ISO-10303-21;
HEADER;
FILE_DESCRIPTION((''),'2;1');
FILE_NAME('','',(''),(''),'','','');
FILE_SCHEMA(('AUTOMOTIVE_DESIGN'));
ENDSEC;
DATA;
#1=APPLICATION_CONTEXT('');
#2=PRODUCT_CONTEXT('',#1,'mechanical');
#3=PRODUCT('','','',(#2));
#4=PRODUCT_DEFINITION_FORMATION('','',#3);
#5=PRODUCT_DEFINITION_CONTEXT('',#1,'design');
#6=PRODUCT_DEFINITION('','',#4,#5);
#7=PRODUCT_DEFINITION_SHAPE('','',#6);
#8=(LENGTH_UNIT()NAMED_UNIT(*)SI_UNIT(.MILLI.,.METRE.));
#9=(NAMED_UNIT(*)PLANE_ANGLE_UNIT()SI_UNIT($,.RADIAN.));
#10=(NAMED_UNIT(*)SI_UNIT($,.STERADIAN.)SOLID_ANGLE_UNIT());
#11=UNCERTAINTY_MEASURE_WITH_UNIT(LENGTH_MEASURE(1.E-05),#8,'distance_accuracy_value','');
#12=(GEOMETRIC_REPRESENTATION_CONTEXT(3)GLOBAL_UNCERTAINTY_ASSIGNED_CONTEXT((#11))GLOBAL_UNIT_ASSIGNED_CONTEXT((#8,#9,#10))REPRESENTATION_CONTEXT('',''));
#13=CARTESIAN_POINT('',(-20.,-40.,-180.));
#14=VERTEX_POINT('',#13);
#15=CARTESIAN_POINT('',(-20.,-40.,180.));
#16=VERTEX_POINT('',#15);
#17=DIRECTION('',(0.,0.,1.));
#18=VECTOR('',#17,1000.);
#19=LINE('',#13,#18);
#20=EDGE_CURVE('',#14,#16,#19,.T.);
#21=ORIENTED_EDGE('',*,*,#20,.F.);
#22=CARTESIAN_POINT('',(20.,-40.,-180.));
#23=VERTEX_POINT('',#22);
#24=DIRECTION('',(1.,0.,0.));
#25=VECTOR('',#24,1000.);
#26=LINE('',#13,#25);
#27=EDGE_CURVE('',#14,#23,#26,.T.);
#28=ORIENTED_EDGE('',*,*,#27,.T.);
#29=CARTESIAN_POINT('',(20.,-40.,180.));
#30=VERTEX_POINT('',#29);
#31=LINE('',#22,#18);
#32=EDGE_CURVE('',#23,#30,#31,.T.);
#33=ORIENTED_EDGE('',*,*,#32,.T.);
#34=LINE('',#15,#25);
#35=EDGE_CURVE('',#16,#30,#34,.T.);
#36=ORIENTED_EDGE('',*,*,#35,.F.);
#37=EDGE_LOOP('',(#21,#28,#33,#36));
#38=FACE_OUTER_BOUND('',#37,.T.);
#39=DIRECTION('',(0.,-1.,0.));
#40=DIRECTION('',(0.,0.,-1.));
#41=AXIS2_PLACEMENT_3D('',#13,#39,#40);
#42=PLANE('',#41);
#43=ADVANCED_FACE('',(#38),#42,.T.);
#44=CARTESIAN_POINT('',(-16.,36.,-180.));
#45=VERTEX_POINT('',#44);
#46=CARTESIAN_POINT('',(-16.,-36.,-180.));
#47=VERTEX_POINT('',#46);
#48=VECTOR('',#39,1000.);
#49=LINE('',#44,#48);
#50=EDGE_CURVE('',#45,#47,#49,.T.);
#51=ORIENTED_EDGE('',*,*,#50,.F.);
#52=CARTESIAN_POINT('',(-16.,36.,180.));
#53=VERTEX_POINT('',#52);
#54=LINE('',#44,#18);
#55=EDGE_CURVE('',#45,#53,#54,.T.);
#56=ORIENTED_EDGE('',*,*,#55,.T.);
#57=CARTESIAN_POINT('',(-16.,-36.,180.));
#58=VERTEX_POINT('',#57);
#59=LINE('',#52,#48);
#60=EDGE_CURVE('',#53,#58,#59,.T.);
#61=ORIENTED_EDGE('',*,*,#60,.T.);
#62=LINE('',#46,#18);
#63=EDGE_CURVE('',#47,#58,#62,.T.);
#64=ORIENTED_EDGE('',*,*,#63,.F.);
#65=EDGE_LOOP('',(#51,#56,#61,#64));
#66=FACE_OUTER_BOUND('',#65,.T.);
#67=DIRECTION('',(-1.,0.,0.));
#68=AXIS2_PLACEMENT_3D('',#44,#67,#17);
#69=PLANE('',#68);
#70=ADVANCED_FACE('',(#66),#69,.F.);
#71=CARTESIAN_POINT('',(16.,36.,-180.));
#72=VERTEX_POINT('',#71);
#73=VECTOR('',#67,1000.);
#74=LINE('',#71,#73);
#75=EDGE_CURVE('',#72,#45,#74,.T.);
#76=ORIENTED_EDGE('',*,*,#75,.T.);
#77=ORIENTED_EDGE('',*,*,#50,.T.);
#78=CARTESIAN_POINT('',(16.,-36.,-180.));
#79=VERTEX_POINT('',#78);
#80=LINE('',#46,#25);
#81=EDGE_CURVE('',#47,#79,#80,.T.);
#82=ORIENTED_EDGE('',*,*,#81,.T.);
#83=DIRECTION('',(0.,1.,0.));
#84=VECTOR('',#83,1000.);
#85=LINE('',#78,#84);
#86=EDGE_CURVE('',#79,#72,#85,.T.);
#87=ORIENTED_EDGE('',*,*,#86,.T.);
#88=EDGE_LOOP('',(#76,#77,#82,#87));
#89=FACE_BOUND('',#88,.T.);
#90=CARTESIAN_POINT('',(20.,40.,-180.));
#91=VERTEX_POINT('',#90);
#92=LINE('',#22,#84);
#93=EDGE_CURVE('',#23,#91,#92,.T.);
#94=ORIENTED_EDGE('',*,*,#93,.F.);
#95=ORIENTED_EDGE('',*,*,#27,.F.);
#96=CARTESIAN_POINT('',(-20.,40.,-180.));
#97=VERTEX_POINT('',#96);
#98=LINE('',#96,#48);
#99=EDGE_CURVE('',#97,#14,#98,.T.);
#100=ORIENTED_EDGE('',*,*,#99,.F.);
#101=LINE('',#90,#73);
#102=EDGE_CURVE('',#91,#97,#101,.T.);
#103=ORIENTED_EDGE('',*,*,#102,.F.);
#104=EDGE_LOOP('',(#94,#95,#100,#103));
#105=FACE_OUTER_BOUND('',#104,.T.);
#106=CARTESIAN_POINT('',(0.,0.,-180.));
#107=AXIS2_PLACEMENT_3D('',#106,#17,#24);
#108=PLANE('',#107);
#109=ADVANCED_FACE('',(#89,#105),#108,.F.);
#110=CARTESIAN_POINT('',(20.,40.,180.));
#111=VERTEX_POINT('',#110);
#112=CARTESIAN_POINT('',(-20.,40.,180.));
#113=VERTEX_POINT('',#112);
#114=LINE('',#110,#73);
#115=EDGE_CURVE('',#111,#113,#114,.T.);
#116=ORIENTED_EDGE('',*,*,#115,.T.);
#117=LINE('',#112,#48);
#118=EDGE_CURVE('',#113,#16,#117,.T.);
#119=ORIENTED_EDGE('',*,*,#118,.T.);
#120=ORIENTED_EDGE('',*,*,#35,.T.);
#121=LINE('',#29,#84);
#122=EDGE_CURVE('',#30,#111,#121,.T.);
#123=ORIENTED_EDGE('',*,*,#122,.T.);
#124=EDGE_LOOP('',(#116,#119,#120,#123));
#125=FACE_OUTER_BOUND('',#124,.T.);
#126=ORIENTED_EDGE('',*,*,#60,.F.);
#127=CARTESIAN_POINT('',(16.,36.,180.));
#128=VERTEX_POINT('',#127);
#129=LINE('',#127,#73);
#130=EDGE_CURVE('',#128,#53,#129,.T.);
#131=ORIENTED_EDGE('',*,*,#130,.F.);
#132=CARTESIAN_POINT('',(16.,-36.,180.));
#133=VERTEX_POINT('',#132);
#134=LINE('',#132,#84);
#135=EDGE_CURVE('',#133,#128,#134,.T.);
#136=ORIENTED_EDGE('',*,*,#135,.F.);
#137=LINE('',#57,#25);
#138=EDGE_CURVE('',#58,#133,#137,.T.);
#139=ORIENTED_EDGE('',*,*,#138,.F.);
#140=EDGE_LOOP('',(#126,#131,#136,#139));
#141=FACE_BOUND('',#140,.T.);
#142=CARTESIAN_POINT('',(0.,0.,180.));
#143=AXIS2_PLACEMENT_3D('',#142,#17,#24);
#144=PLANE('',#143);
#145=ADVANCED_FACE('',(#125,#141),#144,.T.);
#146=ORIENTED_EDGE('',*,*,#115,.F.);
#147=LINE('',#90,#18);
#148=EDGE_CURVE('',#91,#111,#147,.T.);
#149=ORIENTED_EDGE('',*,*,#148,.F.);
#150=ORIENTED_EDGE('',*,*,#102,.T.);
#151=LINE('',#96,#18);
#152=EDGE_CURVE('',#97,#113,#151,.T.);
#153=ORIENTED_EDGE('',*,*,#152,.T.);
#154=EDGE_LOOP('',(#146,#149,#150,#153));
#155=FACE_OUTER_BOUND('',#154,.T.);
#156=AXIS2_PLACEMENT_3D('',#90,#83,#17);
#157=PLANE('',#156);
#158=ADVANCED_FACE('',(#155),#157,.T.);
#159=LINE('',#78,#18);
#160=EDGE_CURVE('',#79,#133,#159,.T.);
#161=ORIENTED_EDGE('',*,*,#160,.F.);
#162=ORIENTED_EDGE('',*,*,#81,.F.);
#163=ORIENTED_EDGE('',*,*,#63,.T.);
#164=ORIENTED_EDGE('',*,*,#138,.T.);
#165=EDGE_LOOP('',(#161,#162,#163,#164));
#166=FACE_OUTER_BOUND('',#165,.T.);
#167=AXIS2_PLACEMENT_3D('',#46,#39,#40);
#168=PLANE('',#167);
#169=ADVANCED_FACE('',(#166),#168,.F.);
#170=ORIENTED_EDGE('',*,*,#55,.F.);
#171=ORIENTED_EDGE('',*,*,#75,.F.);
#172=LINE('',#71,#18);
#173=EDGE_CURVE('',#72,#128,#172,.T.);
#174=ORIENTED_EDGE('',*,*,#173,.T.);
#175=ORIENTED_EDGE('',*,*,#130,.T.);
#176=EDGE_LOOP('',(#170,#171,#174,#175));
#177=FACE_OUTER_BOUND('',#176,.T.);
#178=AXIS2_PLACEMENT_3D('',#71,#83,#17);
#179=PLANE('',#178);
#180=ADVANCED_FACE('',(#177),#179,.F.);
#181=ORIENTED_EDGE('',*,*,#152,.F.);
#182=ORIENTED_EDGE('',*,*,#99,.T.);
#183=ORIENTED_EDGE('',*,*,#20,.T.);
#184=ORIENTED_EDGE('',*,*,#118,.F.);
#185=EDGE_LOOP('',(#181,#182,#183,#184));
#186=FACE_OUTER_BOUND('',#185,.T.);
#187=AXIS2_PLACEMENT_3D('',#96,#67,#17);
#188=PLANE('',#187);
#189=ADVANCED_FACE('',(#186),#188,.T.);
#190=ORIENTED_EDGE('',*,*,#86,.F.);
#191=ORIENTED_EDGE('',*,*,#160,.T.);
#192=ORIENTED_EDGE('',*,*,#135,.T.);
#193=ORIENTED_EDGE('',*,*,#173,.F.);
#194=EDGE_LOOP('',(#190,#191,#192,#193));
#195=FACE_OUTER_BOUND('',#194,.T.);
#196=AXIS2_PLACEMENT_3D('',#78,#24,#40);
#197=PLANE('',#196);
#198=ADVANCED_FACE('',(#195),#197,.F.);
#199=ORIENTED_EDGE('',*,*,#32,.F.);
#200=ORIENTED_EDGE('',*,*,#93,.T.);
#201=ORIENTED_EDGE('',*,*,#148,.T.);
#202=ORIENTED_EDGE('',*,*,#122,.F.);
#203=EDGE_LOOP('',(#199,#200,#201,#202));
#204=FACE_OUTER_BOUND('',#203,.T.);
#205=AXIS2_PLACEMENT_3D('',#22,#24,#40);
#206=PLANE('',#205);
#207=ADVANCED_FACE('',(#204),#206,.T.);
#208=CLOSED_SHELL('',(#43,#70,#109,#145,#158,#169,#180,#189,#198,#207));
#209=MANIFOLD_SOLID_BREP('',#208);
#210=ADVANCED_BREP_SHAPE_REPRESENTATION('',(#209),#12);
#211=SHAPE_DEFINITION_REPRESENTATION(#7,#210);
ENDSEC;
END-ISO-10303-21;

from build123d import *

# Parameters (mm, degrees)
SKETCH_1_W      = 40
SKETCH_1_H      = 80
SKETCH_1_W_2    = 32
SKETCH_1_H_2    = 72
EXTRUDE_1_DEPTH = 180


with BuildPart() as part:
    # 草图1 → 凸台-拉伸1 (new, symmetric)
    with BuildSketch(Plane.XY):
        Rectangle(SKETCH_1_W, SKETCH_1_H)
        Rectangle(SKETCH_1_W_2, SKETCH_1_H_2, mode=Mode.SUBTRACT)
    extrude(amount=EXTRUDE_1_DEPTH, both=True)


solid = part.part
